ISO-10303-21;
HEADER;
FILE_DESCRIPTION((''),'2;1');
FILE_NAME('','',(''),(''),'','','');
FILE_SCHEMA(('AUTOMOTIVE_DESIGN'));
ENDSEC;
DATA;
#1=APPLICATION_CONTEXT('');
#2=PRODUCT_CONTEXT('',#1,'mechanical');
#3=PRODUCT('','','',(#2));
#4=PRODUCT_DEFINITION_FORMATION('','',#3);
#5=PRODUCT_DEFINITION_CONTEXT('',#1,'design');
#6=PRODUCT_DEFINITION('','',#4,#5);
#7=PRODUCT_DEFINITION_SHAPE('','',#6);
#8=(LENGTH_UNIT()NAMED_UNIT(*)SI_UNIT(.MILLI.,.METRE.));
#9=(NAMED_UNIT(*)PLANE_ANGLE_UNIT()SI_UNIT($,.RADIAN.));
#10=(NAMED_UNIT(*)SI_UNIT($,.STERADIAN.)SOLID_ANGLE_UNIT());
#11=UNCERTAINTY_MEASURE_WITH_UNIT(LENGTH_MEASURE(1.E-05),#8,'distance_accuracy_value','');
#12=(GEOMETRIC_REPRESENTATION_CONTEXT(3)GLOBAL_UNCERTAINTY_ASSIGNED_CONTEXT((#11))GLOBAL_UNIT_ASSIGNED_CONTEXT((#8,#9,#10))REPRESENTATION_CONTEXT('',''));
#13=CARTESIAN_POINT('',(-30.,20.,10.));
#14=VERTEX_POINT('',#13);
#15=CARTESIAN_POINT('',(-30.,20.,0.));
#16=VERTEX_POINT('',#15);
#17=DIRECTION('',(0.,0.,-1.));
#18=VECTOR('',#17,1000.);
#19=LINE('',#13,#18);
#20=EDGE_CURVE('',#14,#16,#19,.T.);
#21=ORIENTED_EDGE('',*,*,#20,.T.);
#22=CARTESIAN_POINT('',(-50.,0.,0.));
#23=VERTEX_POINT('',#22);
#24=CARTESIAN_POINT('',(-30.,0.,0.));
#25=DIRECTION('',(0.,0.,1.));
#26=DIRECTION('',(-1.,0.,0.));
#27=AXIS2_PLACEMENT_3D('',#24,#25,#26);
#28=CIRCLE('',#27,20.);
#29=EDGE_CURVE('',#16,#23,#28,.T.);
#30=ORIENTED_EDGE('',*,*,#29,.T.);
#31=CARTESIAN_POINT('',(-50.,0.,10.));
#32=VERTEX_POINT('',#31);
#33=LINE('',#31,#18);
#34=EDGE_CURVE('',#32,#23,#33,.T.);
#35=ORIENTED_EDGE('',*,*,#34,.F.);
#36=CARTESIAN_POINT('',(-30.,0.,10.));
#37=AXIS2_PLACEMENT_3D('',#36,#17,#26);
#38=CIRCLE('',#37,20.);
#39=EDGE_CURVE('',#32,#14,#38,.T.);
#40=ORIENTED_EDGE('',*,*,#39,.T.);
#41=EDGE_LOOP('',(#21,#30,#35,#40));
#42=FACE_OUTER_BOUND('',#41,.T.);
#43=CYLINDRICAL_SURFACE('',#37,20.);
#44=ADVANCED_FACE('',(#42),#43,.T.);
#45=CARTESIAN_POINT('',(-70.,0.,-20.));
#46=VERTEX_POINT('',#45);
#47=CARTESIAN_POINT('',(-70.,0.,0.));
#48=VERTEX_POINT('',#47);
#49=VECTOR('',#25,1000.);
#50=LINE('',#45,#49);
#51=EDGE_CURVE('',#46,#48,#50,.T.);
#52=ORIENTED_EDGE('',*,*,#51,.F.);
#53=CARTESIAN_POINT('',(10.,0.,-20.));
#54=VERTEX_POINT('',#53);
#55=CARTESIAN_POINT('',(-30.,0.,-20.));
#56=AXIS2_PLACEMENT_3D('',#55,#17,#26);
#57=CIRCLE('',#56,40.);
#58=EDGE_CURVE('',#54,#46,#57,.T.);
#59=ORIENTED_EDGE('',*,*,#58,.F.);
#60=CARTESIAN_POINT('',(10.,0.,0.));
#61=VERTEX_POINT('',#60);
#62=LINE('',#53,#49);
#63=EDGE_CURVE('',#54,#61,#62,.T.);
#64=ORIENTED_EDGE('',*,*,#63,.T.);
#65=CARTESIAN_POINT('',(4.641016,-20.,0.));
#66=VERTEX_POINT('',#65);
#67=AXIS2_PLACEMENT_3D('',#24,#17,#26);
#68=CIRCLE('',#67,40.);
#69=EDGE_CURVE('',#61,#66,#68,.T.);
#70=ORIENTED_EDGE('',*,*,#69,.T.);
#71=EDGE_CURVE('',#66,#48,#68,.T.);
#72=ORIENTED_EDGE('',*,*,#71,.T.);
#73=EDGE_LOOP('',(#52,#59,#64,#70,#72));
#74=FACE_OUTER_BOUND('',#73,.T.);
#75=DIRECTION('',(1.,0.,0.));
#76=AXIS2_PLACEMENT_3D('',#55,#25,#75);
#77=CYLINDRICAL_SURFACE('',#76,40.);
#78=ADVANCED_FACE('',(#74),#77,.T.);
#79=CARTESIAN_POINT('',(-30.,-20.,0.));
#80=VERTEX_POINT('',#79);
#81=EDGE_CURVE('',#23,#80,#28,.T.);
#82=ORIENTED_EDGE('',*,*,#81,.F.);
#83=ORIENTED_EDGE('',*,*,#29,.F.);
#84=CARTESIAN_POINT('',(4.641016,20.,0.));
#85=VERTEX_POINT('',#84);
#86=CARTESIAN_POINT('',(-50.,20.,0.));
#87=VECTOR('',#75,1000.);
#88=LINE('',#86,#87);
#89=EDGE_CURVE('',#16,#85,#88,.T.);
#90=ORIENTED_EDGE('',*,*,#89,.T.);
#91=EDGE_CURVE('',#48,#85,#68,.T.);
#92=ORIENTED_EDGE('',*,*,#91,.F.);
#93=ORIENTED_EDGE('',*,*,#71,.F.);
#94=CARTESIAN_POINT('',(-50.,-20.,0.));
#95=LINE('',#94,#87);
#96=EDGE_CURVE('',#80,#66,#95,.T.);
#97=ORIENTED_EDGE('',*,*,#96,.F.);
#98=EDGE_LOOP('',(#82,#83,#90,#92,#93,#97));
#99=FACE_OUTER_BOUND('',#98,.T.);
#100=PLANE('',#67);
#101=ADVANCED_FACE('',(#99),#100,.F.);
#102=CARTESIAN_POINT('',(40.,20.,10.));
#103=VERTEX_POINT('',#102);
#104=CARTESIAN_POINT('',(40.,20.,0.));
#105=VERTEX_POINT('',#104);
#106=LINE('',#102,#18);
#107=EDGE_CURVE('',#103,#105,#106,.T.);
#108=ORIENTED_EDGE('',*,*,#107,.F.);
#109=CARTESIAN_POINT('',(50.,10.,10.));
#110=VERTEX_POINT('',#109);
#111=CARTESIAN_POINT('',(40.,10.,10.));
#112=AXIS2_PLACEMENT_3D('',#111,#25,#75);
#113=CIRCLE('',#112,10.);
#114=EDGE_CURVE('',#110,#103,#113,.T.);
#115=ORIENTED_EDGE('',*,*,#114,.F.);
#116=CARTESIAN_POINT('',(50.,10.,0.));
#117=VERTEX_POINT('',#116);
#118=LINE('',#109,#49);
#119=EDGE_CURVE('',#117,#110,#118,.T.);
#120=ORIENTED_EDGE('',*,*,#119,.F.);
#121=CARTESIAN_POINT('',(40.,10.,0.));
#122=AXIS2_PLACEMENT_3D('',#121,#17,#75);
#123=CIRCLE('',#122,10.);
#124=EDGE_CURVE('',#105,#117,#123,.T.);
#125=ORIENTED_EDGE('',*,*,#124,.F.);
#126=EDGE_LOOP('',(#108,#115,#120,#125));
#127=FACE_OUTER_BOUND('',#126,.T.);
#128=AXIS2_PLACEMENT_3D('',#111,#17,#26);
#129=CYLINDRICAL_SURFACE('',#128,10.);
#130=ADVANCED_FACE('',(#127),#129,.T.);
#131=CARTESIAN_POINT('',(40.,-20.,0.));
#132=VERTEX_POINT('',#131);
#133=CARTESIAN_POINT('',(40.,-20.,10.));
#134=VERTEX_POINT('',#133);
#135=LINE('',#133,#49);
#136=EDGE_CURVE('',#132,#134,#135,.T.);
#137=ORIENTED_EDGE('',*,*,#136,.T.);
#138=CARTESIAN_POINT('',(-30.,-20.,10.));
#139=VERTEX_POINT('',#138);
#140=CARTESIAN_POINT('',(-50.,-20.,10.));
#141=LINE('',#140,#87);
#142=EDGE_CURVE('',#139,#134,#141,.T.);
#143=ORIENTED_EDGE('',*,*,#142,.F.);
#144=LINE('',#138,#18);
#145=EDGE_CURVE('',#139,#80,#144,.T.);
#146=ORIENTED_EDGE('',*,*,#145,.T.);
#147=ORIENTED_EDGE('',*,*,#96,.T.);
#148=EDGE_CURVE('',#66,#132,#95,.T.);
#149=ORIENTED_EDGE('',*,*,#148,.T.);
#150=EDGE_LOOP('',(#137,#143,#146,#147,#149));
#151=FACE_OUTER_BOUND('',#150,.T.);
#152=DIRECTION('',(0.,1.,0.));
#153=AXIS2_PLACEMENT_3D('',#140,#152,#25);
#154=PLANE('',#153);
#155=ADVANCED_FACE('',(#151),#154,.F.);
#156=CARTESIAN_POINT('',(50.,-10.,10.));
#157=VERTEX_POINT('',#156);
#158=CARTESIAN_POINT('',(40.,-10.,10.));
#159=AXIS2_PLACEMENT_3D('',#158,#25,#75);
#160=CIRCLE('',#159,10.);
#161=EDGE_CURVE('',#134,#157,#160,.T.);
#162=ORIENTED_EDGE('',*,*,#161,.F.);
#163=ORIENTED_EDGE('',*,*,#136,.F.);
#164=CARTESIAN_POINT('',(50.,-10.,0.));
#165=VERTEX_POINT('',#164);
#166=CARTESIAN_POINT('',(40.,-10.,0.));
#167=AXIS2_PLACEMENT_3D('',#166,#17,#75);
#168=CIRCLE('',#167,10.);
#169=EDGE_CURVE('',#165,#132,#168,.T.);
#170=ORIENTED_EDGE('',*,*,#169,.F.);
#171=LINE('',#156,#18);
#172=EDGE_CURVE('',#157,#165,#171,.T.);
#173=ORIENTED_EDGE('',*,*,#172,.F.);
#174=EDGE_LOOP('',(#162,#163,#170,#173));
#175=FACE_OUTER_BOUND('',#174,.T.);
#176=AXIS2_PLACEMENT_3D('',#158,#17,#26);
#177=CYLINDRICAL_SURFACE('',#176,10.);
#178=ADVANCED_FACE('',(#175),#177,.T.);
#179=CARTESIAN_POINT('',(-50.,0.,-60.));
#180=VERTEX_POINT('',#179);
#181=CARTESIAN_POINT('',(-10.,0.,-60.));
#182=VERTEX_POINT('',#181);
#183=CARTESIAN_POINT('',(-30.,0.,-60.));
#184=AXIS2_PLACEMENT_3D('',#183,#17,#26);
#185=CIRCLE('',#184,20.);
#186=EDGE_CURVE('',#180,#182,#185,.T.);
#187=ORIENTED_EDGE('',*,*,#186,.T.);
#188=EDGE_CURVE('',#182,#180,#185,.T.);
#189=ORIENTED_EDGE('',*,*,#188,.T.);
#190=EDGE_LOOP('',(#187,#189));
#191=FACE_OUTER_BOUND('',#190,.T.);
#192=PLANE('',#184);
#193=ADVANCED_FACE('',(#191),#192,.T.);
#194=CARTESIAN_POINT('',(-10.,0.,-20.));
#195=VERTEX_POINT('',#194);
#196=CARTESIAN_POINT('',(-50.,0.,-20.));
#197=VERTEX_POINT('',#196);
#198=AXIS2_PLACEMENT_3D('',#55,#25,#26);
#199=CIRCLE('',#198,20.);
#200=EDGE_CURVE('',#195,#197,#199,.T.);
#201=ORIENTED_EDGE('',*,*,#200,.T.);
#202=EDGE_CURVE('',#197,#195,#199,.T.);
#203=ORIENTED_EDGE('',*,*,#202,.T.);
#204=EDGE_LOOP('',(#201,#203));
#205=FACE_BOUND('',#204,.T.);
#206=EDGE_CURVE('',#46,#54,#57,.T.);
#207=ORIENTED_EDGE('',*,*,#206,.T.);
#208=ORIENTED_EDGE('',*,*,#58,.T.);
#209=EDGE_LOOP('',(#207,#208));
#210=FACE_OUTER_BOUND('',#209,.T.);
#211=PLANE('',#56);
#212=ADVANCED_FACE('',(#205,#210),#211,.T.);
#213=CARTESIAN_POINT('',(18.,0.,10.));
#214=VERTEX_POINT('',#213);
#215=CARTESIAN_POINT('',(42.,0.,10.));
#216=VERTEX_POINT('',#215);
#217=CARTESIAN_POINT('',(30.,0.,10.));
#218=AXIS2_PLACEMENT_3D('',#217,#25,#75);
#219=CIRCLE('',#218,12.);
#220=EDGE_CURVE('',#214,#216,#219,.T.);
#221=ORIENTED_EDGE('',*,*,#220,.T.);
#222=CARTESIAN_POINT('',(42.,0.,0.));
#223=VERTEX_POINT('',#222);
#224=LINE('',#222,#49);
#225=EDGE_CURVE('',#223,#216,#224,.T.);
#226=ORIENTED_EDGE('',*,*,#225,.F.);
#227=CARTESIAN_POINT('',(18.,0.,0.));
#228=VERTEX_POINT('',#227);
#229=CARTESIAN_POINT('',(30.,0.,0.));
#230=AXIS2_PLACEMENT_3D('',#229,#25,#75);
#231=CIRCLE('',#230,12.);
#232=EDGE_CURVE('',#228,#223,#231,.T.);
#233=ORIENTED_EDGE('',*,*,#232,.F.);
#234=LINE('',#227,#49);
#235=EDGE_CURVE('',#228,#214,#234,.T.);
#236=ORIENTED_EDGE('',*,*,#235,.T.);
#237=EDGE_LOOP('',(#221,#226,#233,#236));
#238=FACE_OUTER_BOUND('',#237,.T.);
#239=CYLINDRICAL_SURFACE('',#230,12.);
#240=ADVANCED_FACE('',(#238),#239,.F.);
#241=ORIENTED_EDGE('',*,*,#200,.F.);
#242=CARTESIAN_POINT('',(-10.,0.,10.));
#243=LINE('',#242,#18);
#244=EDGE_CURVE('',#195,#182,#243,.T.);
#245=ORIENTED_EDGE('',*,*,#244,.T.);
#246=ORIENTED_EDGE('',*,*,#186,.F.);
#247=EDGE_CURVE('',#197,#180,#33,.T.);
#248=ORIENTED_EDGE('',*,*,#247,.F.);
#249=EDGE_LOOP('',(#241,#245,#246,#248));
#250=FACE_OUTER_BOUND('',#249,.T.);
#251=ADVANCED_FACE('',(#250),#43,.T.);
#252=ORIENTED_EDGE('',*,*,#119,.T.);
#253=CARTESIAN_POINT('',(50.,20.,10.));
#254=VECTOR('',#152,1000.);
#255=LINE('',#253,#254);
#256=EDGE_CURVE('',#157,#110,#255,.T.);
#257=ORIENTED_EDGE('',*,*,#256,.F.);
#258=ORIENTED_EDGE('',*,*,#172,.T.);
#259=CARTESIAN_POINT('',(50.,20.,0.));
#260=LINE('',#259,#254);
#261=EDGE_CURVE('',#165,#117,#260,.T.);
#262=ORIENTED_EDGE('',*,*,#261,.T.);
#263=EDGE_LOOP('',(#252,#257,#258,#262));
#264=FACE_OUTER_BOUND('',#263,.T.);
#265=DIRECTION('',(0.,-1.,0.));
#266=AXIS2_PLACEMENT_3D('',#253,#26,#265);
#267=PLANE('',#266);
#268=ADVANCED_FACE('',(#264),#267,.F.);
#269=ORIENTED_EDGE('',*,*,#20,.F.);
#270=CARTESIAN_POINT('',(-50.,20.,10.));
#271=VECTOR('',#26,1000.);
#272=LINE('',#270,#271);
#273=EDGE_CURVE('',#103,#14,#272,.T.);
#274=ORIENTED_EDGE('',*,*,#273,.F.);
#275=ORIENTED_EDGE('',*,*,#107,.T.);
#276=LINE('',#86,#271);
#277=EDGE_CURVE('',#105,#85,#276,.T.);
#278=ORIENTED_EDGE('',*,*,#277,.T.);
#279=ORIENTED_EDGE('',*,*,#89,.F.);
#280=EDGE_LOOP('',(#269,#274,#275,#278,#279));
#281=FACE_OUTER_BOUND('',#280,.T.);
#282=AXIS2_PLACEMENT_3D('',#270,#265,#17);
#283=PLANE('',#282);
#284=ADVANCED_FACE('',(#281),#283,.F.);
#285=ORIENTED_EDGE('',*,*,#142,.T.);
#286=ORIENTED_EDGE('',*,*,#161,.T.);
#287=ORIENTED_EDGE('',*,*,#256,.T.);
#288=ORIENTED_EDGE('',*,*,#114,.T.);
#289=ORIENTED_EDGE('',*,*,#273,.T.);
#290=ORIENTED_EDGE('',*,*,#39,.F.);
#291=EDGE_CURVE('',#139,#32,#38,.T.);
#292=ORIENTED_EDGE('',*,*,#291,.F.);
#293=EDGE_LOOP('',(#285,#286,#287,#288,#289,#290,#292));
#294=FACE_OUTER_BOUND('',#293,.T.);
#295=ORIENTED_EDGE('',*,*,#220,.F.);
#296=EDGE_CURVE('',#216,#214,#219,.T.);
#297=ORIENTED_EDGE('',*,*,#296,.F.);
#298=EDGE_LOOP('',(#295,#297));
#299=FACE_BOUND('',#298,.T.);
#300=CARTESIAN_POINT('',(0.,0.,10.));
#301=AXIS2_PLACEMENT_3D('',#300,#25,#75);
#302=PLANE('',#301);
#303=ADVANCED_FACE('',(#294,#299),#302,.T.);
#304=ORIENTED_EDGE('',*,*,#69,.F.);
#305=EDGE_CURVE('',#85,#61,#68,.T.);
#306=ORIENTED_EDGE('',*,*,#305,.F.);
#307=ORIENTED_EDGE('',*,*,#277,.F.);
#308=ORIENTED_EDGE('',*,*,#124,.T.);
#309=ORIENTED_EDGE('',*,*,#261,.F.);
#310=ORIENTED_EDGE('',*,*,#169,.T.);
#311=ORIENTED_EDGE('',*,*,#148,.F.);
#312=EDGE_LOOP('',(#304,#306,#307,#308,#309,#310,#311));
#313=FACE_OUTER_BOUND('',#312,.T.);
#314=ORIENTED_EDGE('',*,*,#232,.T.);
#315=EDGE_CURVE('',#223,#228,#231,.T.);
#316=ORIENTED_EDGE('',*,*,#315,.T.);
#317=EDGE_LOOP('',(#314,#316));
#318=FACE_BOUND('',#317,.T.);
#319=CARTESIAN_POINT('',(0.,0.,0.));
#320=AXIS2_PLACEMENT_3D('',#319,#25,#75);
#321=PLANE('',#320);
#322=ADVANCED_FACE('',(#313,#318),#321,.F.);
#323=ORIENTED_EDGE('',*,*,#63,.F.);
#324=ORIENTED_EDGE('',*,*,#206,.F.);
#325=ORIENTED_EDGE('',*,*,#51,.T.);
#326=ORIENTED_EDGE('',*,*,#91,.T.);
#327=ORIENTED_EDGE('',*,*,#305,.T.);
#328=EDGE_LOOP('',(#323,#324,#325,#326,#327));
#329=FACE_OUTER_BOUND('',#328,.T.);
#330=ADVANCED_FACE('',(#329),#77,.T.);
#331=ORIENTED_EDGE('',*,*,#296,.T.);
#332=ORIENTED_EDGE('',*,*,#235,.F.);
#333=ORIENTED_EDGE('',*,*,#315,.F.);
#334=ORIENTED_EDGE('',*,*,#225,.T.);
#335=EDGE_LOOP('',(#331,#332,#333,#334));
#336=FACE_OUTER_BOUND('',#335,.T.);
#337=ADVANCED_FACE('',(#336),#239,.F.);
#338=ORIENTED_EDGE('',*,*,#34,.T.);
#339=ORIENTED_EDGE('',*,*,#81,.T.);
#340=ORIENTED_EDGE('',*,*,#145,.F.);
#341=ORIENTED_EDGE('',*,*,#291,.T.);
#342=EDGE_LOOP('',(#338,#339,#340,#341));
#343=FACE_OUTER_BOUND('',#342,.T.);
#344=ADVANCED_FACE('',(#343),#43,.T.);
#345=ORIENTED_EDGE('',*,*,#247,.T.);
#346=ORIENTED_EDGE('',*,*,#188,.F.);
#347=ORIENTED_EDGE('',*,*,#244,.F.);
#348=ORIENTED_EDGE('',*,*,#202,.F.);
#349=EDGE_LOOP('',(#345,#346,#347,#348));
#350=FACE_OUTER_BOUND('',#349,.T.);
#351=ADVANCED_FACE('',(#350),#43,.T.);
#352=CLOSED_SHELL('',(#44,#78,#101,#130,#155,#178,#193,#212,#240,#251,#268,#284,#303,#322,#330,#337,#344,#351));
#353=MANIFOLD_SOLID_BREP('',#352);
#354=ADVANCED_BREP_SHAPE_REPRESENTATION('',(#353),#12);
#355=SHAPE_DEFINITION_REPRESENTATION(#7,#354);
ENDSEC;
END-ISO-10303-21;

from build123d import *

# Parameters (mm, degrees)
SKETCH1_W           = 100
SKETCH1_H           = 40
BOSS_EXTRUDE1_DEPTH = 10
SKETCH2_R           = 12
CUT_EXTRUDE1_DEPTH  = 10
FILLET1_R           = 10
CUT_EXTRUDE2_DEPTH  = 10
BOSS_EXTRUDE2_START = 60
SKETCH4_R           = 20
BOSS_EXTRUDE2_DEPTH = 60
SKETCH5_R           = 40
BOSS_EXTRUDE3_DEPTH = 20


with BuildPart() as part:
    # Sketch1 → Boss-Extrude1 (new body)
    with BuildSketch(Plane.XY):
        Rectangle(SKETCH1_W, SKETCH1_H)
    extrude(amount=BOSS_EXTRUDE1_DEPTH)

    # Sketch2 → Cut-Extrude1 (cut)
    with BuildSketch(Plane.XY.offset(10)):
        with Locations((30, 0)):
            Circle(SKETCH2_R)
    extrude(amount=-CUT_EXTRUDE1_DEPTH, mode=Mode.SUBTRACT)

    # Fillet1
    fillet1_edges = [part.edges().sort_by_distance(p)[0] for p in [
        (50, -20, 5),
        (50, 20, 5),
    ]]
    fillet(fillet1_edges, radius=FILLET1_R)

    # Sketch3 → Cut-Extrude2 (cut)
    with BuildSketch(Plane(origin=(0, 0, 0), x_dir=(-1, 0, 0), z_dir=(0, 0, -1))):
        with BuildLine():
            Line((50, 20), (30, 20))
            ThreePointArc((30, 20), (44.142135624, 14.142135624), (50, 0))
            Line((50, 0), (50, 20))
        make_face()
        with BuildLine():
            Line((50, -20), (50, 0))
            ThreePointArc((50, 0), (44.142135624, -14.142135624), (30, -20))
            Line((30, -20), (50, -20))
        make_face()
    extrude(amount=-CUT_EXTRUDE2_DEPTH, mode=Mode.SUBTRACT)

    # Sketch4 → Boss-Extrude2 (add)
    with BuildSketch(Plane(origin=(0, 0, 0), x_dir=(-1, 0, 0), z_dir=(0, 0, -1)).offset(BOSS_EXTRUDE2_START)):
        with Locations((30, 0)):
            Circle(SKETCH4_R)
    extrude(amount=-BOSS_EXTRUDE2_DEPTH)

    # Sketch5 → Boss-Extrude3 (add)
    with BuildSketch(Plane(origin=(0, 0, 0), x_dir=(-1, 0, 0), z_dir=(0, 0, -1))):
        with Locations(Location((30, 0, 0), (0, 0, 210))):
            Circle(SKETCH5_R)
    extrude(amount=BOSS_EXTRUDE3_DEPTH)


solid = part.part
